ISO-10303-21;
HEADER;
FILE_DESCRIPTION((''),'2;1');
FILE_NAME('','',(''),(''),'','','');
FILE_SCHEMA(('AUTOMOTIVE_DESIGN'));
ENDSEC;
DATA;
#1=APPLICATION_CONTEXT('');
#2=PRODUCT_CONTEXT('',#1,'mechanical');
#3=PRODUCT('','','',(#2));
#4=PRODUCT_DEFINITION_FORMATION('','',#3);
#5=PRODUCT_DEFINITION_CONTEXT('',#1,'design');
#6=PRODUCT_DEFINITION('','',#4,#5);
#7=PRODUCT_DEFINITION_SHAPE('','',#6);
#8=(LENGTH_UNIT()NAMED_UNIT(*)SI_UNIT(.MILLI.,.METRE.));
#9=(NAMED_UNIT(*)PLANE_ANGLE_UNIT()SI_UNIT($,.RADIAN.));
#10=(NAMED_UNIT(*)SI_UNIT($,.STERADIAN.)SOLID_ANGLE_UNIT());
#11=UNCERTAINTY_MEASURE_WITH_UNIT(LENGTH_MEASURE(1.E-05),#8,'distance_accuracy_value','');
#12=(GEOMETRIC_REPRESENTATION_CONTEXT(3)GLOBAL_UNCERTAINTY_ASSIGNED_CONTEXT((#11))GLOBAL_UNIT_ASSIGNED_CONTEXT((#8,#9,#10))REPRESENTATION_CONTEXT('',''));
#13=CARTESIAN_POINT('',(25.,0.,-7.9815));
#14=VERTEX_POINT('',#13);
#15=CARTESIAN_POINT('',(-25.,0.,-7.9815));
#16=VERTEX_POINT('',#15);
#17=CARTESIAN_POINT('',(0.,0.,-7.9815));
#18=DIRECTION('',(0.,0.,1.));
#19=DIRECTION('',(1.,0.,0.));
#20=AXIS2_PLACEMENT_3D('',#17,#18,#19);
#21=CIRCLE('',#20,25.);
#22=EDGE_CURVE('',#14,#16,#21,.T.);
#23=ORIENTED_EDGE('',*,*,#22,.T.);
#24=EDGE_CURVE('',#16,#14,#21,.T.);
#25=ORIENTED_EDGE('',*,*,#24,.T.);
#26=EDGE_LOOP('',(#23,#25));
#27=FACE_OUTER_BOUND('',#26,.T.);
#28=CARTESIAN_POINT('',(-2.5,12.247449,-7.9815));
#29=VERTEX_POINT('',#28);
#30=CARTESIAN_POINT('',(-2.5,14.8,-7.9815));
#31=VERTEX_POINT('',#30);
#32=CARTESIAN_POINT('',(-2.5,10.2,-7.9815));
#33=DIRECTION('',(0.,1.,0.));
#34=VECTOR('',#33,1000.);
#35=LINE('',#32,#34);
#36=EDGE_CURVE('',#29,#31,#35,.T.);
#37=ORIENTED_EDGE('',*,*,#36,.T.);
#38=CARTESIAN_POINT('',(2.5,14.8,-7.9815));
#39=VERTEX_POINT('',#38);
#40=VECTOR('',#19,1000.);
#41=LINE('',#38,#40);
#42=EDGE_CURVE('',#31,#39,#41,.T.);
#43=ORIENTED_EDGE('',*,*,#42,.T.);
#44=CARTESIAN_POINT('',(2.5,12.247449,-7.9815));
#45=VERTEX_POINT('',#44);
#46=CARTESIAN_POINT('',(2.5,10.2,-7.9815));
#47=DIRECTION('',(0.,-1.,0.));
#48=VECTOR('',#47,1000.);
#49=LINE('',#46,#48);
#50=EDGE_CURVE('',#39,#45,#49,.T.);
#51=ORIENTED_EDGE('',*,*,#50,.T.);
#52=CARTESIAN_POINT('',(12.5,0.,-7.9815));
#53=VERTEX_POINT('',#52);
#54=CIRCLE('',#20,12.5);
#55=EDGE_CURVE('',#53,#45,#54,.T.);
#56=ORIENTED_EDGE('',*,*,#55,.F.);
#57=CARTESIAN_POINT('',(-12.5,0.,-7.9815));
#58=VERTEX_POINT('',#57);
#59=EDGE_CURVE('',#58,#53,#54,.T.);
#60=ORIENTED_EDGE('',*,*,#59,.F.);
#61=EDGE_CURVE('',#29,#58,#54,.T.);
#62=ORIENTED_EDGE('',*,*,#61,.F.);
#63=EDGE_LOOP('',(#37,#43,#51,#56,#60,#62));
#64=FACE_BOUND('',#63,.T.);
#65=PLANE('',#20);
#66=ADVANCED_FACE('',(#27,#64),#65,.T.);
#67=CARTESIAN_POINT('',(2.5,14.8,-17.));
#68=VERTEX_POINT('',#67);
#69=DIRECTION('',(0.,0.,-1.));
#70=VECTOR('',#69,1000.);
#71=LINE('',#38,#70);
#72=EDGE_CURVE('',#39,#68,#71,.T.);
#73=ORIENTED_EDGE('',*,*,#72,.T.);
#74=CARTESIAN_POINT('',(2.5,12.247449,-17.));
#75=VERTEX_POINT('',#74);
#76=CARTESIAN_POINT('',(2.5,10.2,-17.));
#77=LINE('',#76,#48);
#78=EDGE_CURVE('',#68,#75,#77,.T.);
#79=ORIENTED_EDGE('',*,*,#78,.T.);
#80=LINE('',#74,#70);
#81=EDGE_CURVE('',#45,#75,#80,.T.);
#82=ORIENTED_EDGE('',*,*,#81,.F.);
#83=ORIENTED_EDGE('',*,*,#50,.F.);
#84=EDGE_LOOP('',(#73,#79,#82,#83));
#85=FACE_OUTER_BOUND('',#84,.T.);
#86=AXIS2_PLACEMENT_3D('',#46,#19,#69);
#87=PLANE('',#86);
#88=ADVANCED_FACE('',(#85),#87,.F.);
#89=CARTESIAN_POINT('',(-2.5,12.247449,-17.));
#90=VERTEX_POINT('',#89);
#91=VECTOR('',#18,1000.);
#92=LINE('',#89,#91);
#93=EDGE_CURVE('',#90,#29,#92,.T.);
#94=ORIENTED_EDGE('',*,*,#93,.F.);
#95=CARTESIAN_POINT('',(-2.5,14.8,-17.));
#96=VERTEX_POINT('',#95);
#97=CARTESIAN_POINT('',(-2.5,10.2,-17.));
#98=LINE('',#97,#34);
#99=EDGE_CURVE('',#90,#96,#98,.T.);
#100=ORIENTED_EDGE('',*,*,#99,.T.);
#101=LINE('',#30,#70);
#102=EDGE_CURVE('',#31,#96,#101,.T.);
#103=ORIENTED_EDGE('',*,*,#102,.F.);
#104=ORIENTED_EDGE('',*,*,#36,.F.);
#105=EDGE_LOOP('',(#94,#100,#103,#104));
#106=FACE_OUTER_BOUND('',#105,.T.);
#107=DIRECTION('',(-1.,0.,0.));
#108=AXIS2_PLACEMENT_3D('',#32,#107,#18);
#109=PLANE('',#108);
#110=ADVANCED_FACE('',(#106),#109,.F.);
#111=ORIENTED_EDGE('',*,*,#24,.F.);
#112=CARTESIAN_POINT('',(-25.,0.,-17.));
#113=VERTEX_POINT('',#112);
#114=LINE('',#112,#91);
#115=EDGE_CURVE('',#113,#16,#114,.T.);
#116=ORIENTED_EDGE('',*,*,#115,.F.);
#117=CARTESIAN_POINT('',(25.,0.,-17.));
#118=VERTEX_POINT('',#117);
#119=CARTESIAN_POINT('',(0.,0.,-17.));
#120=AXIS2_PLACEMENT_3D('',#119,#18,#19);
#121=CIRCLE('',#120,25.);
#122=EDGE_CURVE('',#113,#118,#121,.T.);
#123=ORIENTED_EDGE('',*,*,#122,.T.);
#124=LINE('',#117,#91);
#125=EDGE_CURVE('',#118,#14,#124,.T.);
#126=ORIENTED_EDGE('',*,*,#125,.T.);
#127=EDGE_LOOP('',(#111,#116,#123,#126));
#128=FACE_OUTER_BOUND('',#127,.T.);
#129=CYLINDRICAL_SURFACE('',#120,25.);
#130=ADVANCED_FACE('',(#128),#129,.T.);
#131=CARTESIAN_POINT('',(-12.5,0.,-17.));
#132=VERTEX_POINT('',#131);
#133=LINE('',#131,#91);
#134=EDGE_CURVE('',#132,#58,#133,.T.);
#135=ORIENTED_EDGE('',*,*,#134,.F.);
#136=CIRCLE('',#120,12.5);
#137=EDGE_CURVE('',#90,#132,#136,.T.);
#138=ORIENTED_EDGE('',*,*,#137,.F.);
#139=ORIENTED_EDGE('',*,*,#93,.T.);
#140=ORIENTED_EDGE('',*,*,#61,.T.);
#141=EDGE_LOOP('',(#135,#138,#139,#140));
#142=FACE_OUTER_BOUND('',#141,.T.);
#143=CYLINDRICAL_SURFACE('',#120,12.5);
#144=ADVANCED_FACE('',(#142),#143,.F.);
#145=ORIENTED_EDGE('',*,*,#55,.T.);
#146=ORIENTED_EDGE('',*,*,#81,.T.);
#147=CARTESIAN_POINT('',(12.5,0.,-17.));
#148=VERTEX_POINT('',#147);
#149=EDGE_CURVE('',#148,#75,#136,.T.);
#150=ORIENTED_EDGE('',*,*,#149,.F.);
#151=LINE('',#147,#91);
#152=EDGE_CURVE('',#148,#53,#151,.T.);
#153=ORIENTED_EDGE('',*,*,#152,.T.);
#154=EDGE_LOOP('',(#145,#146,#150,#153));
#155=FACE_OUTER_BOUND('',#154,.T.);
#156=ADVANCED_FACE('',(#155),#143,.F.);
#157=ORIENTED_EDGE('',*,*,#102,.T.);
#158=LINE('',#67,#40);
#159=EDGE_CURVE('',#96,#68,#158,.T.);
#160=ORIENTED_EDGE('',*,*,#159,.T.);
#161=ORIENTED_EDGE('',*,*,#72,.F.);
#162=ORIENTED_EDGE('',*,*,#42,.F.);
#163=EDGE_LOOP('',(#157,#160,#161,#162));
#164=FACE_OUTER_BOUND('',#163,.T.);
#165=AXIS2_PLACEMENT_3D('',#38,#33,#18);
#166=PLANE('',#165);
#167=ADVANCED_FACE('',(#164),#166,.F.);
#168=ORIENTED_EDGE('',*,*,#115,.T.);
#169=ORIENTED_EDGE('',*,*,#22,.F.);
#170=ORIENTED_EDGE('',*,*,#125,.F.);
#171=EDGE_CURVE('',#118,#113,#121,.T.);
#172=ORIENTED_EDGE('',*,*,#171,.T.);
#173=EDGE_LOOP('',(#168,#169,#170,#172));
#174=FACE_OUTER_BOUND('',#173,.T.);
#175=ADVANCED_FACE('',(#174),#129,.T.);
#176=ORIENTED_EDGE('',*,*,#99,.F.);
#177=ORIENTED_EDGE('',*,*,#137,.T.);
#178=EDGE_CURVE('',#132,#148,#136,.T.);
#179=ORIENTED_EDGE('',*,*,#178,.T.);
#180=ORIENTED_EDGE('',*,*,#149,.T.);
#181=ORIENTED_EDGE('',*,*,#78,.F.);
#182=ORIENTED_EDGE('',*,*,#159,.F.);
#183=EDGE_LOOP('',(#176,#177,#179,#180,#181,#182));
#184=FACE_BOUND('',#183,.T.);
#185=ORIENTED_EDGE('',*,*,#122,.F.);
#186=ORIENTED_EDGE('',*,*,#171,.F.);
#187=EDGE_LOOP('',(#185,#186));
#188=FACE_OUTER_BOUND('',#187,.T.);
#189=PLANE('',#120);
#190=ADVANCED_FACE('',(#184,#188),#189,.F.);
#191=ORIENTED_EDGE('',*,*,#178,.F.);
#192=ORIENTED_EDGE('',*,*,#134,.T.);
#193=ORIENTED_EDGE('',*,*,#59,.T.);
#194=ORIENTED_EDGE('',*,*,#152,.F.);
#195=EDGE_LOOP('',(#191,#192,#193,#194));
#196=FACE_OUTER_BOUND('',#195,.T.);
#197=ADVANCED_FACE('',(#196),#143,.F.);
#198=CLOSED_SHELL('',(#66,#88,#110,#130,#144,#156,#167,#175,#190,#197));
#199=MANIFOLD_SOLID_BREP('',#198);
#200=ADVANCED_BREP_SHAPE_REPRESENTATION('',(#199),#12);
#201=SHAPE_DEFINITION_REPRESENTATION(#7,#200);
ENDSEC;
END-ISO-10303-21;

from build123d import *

# Parameters (mm, degrees)
SKETCH1_R           = 25
SKETCH1_R_2         = 12.5
BOSS_EXTRUDE1_DEPTH = 17
MOVE_FACE1_BY       = 7.981500203
SKETCH2_W           = 5
SKETCH2_H           = 4.6
CUT_EXTRUDE1_DEPTH  = 37.487440834


with BuildPart() as part:
    # Sketch1 → Boss-Extrude1 (new body)
    with BuildSketch(Plane.XY):
        Circle(SKETCH1_R)
        Circle(SKETCH1_R_2, mode=Mode.SUBTRACT)
    extrude(amount=-BOSS_EXTRUDE1_DEPTH)

    # Move Face1: a face moved inward by 7.9815
    extrude(part.faces().sort_by_distance((0, -20, 0))[0], amount=MOVE_FACE1_BY, dir=(0, 0, -1), mode=Mode.SUBTRACT)

    # Sketch2 → Cut-Extrude1 (cut, through all)
    with BuildSketch(Plane(origin=(0, 0, -17), x_dir=(-1, 0, 0), z_dir=(0, 0, -1))):
        with Locations((0, 12.5)):
            Rectangle(SKETCH2_W, SKETCH2_H)
    extrude(amount=-CUT_EXTRUDE1_DEPTH, mode=Mode.SUBTRACT)


solid = part.part
